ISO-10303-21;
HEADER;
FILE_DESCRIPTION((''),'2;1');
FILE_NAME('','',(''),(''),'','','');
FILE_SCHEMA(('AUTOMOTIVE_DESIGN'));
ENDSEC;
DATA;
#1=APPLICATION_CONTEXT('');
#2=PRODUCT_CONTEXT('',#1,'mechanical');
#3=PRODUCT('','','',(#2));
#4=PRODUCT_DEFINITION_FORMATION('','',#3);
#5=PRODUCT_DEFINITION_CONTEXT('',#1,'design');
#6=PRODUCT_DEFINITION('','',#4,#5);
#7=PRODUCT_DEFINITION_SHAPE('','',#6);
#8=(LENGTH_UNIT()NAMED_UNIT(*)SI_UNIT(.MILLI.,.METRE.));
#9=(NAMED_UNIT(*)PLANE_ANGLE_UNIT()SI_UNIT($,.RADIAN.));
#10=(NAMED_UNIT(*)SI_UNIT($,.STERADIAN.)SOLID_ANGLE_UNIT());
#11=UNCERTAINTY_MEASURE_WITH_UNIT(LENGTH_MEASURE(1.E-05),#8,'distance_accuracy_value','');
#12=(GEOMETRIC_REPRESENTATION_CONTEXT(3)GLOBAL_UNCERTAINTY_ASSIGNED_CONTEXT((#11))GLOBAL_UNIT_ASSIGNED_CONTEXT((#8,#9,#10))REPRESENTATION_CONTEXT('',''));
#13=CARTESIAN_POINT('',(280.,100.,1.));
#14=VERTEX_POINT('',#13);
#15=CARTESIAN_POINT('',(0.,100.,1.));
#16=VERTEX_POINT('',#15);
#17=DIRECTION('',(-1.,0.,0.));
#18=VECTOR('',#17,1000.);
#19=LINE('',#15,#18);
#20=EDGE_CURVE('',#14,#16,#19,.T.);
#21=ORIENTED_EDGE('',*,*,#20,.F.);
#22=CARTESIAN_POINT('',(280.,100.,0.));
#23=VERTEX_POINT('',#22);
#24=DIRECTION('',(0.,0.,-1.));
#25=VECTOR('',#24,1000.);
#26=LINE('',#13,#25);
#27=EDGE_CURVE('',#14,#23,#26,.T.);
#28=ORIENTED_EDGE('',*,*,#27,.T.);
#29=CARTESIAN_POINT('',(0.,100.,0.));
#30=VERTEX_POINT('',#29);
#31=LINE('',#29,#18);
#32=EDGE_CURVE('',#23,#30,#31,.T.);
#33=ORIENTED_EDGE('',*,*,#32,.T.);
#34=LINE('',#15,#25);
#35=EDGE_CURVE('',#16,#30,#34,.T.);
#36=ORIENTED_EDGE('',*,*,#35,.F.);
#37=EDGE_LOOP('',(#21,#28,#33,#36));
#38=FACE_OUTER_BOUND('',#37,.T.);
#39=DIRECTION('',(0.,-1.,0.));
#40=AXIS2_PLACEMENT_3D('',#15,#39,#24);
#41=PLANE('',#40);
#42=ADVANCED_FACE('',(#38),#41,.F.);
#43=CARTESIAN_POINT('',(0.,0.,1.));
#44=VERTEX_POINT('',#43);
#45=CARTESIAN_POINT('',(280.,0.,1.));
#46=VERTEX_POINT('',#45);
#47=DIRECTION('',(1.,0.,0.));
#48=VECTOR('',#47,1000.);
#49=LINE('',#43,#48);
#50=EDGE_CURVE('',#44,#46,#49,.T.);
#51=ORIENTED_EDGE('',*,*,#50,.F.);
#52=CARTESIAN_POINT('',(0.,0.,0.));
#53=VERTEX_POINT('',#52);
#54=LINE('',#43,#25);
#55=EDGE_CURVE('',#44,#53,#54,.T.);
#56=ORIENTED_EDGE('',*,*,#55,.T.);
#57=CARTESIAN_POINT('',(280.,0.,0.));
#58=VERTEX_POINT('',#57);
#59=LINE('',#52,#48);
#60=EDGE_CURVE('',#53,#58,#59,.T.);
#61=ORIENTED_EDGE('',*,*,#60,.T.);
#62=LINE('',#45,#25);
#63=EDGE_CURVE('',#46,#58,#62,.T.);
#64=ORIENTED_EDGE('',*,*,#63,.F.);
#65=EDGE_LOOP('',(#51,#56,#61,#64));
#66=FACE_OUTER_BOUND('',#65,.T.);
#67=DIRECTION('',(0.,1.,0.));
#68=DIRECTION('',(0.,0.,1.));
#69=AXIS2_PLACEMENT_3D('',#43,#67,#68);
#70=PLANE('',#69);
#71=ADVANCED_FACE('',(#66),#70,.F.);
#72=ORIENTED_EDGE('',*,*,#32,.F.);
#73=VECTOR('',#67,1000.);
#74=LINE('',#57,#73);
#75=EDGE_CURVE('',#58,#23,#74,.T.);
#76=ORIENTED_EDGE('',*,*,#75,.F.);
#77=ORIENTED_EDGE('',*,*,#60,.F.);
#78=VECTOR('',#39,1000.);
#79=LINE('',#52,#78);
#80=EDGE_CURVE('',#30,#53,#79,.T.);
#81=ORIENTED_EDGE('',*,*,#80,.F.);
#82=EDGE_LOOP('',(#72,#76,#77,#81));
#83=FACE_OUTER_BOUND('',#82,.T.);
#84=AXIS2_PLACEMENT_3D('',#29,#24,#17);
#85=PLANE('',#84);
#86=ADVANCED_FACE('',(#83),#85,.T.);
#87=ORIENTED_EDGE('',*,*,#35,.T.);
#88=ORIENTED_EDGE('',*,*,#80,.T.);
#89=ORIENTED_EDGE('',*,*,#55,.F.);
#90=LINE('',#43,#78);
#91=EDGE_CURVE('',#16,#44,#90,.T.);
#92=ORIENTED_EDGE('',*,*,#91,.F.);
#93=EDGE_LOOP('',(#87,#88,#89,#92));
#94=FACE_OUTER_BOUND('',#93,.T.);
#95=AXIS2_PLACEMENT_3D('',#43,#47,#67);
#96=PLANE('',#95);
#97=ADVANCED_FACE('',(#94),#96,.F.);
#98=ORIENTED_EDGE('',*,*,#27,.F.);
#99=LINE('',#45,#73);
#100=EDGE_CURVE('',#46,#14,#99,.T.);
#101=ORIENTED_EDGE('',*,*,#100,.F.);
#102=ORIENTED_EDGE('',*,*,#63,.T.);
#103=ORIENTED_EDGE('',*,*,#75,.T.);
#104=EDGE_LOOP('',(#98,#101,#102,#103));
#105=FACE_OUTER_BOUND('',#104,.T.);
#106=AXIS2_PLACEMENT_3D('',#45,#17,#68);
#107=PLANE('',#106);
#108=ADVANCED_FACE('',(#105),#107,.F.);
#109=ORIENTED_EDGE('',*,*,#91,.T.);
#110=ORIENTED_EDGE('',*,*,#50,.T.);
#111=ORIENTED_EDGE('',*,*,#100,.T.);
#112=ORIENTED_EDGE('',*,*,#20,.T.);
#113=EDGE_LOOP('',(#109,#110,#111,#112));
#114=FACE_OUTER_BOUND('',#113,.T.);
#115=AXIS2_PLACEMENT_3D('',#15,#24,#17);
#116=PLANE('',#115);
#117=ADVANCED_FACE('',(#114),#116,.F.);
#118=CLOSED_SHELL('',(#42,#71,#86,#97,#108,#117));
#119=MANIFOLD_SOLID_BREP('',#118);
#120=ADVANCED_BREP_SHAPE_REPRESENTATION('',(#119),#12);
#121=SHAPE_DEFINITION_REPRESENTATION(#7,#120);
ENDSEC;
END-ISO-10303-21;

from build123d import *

# Parameters (mm, degrees)
SKETCH_1_W      = 280
SKETCH_1_H      = 100
EXTRUDE_1_DEPTH = 1


with BuildPart() as part:
    # 草图1 → 凸台-拉伸1 (new body)
    with BuildSketch(Plane.XY):
        with Locations((140, 50)):
            Rectangle(SKETCH_1_W, SKETCH_1_H)
    extrude(amount=EXTRUDE_1_DEPTH)


solid = part.part
